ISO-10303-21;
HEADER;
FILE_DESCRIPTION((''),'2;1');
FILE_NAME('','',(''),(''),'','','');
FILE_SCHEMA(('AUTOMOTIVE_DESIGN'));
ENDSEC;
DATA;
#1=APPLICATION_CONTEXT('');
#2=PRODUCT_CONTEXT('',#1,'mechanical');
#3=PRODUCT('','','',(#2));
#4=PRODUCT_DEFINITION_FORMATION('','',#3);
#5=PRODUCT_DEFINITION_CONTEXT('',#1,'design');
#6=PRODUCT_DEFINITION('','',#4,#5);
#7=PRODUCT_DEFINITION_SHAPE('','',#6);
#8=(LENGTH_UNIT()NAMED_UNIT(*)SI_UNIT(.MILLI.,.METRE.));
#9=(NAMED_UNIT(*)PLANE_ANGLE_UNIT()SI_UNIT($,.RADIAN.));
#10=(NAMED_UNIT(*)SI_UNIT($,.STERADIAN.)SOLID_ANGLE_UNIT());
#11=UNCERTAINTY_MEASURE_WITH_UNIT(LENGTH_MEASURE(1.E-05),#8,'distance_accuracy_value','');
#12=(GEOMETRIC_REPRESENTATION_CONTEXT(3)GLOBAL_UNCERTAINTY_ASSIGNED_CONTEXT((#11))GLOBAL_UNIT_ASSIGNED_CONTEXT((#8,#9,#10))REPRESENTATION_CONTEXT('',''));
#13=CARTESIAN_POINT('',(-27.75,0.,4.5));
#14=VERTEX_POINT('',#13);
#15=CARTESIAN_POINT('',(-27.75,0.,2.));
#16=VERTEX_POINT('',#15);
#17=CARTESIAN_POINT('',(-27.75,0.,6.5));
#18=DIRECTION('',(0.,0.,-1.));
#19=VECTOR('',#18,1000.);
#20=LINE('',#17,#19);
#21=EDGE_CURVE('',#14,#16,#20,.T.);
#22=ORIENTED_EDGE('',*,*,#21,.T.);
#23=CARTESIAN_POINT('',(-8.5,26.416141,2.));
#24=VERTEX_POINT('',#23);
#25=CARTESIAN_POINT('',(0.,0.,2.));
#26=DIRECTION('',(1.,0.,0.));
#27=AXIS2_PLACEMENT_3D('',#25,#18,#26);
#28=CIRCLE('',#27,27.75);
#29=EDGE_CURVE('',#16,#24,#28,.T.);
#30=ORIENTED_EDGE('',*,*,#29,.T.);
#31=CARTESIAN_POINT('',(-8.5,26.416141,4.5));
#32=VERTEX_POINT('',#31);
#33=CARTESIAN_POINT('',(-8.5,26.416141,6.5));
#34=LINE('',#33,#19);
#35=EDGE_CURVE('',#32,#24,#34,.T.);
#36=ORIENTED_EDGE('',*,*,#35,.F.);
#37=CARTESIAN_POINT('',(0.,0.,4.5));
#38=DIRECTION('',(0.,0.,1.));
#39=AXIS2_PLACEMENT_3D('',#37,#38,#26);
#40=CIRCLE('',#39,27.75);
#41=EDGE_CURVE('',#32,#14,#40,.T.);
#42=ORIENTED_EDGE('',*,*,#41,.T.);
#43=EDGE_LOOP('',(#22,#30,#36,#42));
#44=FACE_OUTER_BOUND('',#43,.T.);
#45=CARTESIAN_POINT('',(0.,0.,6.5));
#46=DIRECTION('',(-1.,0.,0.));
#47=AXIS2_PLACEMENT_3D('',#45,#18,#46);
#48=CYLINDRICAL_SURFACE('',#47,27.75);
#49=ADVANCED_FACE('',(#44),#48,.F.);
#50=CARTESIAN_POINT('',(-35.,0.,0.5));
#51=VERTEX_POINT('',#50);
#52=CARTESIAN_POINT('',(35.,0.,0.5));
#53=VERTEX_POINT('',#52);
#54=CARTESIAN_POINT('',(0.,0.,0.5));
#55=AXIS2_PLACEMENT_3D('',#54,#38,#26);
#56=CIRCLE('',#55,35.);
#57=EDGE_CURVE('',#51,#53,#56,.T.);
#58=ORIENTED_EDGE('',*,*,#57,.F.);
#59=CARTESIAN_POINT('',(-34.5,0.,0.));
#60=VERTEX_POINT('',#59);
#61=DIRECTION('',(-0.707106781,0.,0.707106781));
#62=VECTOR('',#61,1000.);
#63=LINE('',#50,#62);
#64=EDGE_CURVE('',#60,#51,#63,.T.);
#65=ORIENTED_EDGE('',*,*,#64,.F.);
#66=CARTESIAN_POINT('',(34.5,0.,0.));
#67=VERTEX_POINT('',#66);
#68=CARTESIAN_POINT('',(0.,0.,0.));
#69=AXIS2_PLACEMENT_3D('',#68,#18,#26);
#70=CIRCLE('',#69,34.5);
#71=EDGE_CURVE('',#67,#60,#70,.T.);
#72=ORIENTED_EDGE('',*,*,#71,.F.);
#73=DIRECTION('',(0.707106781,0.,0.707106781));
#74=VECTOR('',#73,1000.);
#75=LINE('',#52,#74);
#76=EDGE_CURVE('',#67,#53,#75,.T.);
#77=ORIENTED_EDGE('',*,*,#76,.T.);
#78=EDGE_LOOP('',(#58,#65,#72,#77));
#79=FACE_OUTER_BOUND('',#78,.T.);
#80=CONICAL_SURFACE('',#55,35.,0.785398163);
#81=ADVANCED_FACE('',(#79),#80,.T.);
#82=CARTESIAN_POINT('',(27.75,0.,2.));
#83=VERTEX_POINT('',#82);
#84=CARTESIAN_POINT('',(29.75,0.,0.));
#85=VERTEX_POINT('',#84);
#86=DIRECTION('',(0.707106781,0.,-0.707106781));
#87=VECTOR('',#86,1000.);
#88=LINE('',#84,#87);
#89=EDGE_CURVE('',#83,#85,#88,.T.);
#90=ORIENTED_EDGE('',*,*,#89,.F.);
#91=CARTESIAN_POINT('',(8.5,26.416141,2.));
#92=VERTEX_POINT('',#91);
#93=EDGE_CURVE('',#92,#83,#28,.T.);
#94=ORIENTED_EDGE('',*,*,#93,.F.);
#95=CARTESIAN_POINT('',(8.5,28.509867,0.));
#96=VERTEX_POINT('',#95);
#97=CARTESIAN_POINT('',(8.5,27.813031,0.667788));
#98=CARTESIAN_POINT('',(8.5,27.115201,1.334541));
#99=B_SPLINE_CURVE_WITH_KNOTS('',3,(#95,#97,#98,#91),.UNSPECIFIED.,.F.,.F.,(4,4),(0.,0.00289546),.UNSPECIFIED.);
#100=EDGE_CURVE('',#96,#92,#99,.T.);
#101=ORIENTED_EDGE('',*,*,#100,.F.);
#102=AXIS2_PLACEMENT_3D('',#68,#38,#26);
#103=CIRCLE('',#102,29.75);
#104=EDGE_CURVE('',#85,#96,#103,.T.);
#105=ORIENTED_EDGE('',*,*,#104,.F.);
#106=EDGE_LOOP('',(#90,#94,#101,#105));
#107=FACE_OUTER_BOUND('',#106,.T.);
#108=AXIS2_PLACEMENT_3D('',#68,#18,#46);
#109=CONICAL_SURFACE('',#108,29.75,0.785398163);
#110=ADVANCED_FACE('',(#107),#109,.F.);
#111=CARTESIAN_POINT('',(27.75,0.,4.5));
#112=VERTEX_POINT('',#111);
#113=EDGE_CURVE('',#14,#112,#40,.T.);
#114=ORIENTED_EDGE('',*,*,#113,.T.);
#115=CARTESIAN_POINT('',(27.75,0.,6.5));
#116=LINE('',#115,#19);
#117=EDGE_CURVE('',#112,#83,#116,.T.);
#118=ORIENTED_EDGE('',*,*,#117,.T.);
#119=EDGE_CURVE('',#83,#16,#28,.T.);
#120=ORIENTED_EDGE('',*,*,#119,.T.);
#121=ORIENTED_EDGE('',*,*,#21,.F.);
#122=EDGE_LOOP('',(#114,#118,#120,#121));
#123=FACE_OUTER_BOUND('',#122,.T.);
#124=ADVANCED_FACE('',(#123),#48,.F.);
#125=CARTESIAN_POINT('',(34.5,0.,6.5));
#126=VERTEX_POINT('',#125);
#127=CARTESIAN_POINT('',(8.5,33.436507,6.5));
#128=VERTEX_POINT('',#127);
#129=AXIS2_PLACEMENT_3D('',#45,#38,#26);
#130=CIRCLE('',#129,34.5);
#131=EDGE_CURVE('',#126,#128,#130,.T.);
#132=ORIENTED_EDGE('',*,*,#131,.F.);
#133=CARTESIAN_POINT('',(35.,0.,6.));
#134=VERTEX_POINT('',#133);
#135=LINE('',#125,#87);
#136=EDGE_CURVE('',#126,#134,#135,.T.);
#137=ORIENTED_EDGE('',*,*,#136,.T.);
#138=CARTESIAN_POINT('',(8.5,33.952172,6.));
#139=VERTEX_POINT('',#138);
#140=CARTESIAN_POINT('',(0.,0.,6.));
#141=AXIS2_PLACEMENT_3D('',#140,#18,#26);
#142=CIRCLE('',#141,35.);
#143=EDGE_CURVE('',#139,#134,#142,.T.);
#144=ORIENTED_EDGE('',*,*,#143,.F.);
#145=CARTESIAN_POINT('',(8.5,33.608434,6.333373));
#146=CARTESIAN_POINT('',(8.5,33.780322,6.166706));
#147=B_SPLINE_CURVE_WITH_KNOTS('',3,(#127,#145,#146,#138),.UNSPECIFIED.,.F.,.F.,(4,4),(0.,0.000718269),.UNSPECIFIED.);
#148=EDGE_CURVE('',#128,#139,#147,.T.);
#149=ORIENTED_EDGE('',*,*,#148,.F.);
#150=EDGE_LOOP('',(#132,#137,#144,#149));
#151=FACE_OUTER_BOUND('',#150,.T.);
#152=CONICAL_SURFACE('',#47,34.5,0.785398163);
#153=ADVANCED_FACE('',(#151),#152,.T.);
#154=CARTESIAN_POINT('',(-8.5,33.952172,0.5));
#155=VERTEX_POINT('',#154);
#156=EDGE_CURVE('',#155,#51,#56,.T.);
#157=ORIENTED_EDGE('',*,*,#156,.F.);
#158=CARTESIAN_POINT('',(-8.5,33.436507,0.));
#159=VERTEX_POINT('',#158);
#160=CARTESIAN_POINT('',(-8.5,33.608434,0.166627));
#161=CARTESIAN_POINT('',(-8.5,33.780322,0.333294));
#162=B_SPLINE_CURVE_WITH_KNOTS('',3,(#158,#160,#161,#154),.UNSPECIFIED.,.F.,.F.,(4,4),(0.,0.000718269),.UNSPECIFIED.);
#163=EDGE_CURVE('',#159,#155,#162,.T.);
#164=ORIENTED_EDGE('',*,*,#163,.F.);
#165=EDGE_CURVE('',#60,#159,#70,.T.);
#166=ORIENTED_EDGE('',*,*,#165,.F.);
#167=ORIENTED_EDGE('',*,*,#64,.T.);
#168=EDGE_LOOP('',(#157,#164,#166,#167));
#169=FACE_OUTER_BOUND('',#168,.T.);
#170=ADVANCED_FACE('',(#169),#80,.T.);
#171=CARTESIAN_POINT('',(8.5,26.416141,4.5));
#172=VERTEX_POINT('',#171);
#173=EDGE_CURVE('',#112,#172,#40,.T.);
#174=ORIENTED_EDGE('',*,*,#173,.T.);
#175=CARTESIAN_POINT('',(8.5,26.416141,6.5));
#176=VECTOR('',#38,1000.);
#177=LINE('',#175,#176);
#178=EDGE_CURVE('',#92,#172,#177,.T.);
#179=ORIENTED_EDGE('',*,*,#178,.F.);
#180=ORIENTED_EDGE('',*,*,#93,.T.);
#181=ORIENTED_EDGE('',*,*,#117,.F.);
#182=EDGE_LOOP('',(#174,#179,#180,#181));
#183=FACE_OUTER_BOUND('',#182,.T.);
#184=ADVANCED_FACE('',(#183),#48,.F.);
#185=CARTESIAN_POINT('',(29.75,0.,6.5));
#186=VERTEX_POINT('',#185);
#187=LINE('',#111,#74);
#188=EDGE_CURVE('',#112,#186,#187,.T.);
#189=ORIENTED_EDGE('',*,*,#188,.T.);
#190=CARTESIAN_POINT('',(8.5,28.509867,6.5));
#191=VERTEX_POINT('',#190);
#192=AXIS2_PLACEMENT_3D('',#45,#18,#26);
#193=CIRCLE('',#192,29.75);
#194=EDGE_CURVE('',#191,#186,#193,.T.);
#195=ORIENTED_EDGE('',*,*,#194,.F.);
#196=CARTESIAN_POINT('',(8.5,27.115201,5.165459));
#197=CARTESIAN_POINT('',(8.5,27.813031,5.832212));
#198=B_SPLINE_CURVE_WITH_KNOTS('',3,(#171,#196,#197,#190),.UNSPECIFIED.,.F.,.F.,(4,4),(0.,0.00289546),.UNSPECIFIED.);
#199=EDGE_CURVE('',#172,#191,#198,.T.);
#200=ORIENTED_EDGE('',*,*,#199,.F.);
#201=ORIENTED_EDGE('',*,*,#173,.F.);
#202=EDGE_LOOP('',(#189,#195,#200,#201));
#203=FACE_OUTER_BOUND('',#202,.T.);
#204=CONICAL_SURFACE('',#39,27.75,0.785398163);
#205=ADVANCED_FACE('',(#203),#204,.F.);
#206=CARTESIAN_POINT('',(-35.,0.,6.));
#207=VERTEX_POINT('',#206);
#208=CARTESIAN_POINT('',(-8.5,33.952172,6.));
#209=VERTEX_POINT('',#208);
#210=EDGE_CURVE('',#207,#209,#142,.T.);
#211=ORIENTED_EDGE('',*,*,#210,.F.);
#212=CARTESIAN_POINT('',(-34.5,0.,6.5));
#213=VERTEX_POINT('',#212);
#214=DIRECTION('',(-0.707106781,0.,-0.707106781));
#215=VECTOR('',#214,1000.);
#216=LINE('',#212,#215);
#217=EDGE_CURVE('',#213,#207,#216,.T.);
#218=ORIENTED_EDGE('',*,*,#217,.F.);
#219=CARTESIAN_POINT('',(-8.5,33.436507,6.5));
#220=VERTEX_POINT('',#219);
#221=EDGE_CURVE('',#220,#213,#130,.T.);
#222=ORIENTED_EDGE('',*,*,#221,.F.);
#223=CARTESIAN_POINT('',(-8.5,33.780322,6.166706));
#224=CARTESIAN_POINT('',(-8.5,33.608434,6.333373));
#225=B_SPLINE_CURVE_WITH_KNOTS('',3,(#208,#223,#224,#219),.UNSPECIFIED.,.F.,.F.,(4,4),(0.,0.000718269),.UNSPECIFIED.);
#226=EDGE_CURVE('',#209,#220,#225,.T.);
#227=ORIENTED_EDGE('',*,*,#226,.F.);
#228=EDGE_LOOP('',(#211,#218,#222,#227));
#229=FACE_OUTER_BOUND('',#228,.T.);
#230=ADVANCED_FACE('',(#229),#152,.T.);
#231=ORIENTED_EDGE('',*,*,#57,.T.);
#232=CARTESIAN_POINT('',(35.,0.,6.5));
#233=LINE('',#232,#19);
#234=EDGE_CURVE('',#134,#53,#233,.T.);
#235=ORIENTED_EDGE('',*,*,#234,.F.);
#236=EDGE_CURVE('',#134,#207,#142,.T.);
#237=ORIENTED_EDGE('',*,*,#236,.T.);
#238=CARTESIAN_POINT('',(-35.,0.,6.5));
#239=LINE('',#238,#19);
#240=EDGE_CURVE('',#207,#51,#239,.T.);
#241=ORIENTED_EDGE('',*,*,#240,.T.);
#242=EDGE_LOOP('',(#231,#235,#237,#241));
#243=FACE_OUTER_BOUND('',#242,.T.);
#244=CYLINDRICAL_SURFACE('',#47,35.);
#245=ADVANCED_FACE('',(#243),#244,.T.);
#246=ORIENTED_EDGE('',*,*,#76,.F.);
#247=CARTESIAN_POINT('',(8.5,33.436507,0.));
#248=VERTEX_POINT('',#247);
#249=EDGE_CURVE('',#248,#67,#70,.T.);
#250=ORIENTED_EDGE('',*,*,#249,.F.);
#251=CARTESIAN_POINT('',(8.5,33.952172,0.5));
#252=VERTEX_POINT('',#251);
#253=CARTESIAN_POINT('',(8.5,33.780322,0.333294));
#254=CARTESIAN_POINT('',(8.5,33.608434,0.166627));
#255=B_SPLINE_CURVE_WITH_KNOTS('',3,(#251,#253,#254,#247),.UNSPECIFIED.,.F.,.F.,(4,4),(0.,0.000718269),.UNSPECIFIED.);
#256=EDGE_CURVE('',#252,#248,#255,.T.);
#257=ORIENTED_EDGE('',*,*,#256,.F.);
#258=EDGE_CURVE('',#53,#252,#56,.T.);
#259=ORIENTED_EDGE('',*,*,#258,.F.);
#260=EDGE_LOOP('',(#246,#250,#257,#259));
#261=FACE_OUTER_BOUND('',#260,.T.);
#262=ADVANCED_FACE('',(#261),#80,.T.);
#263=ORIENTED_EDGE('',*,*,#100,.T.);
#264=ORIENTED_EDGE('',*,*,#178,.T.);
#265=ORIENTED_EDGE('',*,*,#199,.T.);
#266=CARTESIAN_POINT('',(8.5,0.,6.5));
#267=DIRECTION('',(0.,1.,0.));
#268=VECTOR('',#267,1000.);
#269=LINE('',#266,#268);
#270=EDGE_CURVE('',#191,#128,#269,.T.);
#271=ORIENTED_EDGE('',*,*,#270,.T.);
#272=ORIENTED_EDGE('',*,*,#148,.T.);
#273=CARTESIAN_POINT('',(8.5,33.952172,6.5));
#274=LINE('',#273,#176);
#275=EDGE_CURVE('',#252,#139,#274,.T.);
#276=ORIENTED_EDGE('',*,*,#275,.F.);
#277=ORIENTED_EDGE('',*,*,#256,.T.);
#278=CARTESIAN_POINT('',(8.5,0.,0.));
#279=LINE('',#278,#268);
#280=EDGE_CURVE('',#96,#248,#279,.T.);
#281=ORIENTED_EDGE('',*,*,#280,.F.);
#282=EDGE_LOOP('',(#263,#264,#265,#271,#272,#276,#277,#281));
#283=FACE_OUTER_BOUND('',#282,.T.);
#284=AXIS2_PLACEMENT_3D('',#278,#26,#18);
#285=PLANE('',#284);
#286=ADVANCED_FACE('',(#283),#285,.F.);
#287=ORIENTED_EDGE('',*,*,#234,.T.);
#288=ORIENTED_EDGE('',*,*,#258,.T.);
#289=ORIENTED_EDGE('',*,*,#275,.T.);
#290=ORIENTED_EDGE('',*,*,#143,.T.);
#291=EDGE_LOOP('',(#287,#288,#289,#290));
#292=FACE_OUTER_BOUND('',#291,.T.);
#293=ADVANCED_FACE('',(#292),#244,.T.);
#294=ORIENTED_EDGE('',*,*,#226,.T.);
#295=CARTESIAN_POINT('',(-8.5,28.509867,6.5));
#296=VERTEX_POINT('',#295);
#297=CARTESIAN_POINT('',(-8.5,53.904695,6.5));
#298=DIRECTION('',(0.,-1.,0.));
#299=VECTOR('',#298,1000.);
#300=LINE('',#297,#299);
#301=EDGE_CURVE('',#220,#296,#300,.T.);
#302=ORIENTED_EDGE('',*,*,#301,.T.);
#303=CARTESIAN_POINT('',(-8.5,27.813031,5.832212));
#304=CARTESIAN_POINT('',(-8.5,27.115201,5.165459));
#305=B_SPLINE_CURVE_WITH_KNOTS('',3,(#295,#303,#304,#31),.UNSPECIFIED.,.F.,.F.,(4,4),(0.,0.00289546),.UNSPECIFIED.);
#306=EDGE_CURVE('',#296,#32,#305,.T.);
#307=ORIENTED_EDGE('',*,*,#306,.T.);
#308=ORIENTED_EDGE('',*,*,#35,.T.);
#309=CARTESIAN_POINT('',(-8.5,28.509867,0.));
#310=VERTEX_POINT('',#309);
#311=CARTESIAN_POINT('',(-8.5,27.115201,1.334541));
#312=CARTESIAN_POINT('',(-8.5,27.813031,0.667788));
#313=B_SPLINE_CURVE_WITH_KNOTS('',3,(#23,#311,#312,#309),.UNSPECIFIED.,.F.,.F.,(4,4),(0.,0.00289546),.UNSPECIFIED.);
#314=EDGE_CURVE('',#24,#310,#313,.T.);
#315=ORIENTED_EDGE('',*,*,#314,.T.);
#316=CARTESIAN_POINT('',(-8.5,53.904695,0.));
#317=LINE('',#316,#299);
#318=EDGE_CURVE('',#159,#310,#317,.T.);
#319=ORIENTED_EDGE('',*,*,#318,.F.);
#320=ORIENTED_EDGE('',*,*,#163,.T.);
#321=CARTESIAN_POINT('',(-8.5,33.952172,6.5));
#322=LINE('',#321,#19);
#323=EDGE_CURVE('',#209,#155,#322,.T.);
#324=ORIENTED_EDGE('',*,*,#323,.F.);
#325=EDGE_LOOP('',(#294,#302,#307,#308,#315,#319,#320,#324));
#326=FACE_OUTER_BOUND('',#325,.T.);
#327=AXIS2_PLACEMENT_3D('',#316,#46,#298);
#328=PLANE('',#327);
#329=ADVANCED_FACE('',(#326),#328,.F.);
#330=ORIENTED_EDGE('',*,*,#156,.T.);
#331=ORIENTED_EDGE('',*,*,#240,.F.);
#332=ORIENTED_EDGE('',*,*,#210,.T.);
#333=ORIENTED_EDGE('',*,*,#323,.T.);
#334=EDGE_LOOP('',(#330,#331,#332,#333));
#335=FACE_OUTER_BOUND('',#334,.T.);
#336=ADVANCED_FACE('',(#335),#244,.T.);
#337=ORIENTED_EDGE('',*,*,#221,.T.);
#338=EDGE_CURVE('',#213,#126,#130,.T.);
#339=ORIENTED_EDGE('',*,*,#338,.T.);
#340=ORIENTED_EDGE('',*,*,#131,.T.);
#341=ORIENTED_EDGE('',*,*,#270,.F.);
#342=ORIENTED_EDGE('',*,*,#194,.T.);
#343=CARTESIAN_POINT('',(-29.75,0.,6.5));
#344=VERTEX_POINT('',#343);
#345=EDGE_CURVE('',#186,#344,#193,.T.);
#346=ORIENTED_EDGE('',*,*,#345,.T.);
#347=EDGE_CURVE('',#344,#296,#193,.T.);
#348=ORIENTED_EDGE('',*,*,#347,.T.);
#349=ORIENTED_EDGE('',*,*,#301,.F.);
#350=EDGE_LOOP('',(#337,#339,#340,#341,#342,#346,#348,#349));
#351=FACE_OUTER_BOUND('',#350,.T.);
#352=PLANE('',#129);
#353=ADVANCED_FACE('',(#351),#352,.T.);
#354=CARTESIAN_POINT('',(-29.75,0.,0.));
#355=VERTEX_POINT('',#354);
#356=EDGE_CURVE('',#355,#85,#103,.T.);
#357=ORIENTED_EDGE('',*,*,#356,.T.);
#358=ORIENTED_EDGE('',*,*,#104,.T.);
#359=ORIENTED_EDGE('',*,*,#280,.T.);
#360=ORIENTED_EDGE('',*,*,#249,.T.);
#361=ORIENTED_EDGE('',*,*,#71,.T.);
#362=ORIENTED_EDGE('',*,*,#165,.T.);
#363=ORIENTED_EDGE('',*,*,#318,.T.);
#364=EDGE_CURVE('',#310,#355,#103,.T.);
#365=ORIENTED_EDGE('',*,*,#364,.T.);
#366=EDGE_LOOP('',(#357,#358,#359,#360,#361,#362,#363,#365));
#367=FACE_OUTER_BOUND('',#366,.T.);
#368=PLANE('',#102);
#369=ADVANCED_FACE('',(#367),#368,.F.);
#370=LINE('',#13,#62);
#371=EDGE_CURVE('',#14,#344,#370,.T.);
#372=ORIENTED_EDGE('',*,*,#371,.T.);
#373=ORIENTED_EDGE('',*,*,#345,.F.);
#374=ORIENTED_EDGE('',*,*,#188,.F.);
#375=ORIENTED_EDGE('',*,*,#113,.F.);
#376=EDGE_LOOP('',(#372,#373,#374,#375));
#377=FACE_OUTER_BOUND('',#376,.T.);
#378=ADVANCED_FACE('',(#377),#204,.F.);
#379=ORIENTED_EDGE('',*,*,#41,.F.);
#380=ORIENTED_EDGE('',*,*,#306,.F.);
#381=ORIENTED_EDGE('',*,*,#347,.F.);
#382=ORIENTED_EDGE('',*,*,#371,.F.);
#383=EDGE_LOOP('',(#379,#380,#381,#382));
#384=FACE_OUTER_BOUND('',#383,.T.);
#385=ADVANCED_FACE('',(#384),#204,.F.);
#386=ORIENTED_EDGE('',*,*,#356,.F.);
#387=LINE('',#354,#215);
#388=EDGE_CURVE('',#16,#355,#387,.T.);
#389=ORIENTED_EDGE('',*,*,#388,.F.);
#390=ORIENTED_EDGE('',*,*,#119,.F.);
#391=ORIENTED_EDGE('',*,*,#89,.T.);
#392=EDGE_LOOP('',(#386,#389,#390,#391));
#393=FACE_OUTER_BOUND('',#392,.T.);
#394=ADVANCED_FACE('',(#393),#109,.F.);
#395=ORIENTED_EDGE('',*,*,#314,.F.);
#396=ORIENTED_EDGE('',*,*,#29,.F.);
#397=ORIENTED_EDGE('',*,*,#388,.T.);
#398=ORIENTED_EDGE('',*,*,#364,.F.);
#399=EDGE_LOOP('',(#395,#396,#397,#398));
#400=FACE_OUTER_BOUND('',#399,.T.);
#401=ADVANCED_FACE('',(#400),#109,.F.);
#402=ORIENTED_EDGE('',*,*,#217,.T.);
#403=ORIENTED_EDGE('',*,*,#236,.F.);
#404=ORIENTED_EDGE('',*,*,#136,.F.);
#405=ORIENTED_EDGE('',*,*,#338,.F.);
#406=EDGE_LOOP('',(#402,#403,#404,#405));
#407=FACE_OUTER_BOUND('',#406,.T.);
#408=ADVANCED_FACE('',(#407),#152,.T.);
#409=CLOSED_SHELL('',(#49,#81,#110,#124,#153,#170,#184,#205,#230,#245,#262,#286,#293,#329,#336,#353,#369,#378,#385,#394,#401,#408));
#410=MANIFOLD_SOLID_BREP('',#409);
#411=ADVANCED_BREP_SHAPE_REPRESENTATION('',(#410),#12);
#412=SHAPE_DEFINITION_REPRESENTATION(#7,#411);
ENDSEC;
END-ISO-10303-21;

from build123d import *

# Parameters (mm, degrees)
SKETCH1_R           = 35
SKETCH1_R_2         = 27.75
BOSS_EXTRUDE1_DEPTH = 6.5
CUT_EXTRUDE1_DEPTH  = 50.922439844
CHAMFER1_SIZE       = 2
CHAMFER2_SIZE       = 0.5


with BuildPart() as part:
    # Sketch1 → Boss-Extrude1 (new body)
    with BuildSketch(Plane.XY):
        with Locations(Location((0, 0, 0), (0, 0, 180))):
            Circle(SKETCH1_R)
        with Locations(Location((0, 0, 0), (0, 0, 180))):
            Circle(SKETCH1_R_2, mode=Mode.SUBTRACT)
    extrude(amount=BOSS_EXTRUDE1_DEPTH)

    # Sketch2 → Cut-Extrude1 (cut, through all)
    with BuildSketch(Plane.XY.offset(6.5)):
        Polygon((0, 0), (8.5, 0), (8.5, 53.904694855), (-8.5, 53.904694855), (-8.5, 0), align=None)
    extrude(amount=-CUT_EXTRUDE1_DEPTH, mode=Mode.SUBTRACT)

    # Chamfer1
    chamfer1_edges = [part.edges().sort_by_distance(p)[0] for p in [
        (0, -27.75, 0),
        (0, -27.75, 6.5),
    ]]
    chamfer(chamfer1_edges, length=CHAMFER1_SIZE)

    # Chamfer2
    chamfer2_edges = [part.edges().sort_by_distance(p)[0] for p in [
        (0, -35, 6.5),
        (0, -35, 0),
    ]]
    chamfer(chamfer2_edges, length=CHAMFER2_SIZE)


solid = part.part
